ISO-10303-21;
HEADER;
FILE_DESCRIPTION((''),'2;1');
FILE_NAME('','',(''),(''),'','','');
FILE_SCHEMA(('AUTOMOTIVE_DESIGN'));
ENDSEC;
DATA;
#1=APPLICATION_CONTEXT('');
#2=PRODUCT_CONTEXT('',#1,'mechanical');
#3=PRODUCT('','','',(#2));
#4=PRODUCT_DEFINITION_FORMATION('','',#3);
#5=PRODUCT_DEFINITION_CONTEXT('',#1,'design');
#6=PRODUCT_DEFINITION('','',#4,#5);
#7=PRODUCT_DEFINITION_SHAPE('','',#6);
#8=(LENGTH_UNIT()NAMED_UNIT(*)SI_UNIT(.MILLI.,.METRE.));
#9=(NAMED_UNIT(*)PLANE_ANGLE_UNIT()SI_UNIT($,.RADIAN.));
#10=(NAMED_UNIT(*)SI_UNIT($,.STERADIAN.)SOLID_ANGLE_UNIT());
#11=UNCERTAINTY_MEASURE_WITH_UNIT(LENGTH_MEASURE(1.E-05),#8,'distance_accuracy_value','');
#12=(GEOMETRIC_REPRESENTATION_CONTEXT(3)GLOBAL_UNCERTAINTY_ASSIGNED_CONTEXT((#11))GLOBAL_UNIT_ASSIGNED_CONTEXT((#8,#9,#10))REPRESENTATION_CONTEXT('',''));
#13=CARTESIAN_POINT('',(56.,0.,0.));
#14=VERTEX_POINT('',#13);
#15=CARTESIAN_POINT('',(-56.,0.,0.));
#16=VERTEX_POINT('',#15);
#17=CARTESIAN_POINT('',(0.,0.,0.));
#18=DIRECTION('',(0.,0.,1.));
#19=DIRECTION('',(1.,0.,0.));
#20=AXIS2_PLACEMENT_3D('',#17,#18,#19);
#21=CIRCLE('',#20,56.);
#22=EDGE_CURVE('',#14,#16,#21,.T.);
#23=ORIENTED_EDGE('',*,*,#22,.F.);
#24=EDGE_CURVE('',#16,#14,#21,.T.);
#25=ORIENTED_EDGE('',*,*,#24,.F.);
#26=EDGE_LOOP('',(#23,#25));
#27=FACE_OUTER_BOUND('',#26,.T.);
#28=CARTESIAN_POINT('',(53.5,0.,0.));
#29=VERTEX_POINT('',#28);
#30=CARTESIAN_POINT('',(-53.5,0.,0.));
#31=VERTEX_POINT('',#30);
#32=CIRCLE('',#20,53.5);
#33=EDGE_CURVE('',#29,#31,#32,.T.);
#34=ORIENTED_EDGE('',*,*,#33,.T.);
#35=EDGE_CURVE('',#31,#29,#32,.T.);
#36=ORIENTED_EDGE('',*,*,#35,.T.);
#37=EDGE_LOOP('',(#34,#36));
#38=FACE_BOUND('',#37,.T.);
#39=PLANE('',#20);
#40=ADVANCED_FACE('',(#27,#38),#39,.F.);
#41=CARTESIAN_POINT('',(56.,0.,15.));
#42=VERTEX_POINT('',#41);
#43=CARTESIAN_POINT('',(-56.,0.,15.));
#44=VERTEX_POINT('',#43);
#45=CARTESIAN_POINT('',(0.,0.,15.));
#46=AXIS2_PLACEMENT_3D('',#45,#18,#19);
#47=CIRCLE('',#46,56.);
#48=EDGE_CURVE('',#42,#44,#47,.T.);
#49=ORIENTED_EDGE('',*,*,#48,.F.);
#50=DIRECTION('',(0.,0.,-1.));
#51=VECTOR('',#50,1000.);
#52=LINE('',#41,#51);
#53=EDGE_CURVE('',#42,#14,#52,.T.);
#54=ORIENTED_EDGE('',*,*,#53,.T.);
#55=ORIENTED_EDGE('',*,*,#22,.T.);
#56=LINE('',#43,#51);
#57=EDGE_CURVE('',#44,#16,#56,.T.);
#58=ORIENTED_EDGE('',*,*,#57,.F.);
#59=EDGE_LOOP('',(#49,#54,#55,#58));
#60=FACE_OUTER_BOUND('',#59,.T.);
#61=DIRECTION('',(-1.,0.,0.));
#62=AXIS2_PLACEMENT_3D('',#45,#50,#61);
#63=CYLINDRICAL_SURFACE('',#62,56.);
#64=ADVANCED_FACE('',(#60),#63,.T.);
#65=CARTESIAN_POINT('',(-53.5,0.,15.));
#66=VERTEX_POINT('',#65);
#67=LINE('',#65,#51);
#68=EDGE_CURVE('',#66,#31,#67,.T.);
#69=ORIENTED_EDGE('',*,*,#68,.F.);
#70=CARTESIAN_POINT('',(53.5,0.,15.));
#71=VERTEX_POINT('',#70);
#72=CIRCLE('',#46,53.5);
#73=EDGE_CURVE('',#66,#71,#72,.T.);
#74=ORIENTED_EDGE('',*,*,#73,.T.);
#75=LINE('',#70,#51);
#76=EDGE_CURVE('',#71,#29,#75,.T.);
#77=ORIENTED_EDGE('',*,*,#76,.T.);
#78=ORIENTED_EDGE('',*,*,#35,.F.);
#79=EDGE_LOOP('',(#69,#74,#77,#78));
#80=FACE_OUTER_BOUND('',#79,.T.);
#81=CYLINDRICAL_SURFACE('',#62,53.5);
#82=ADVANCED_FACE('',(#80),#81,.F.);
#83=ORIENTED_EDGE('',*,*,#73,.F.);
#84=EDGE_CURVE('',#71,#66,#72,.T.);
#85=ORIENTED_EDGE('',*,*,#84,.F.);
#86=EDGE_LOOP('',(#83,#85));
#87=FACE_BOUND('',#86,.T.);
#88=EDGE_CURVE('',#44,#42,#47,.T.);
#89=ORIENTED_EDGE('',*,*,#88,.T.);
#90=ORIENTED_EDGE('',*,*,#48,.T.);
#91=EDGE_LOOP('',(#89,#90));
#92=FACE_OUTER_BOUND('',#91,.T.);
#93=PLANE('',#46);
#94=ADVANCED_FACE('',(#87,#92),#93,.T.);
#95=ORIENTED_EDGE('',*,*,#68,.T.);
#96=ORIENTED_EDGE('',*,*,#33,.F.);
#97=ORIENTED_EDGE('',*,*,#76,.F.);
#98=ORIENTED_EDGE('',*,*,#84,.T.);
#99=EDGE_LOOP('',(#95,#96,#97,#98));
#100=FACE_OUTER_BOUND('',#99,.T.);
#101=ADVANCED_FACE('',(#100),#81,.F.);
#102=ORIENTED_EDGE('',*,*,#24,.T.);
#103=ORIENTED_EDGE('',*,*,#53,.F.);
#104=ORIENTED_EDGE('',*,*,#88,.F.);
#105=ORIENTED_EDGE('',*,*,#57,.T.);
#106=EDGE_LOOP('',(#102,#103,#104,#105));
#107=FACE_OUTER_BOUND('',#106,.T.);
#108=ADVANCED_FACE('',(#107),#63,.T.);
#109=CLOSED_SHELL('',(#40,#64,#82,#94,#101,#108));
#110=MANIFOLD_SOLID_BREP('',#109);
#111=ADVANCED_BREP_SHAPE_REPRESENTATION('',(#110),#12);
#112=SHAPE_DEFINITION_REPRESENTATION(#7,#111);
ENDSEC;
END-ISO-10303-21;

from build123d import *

# Parameters (mm, degrees)
SKETCH1_R           = 56
SKETCH1_R_2         = 53.5
BOSS_EXTRUDE1_DEPTH = 15


with BuildPart() as part:
    # Sketch1 → Boss-Extrude1 (new body)
    with BuildSketch(Plane.XY):
        Circle(SKETCH1_R)
        Circle(SKETCH1_R_2, mode=Mode.SUBTRACT)
    extrude(amount=BOSS_EXTRUDE1_DEPTH)


solid = part.part
